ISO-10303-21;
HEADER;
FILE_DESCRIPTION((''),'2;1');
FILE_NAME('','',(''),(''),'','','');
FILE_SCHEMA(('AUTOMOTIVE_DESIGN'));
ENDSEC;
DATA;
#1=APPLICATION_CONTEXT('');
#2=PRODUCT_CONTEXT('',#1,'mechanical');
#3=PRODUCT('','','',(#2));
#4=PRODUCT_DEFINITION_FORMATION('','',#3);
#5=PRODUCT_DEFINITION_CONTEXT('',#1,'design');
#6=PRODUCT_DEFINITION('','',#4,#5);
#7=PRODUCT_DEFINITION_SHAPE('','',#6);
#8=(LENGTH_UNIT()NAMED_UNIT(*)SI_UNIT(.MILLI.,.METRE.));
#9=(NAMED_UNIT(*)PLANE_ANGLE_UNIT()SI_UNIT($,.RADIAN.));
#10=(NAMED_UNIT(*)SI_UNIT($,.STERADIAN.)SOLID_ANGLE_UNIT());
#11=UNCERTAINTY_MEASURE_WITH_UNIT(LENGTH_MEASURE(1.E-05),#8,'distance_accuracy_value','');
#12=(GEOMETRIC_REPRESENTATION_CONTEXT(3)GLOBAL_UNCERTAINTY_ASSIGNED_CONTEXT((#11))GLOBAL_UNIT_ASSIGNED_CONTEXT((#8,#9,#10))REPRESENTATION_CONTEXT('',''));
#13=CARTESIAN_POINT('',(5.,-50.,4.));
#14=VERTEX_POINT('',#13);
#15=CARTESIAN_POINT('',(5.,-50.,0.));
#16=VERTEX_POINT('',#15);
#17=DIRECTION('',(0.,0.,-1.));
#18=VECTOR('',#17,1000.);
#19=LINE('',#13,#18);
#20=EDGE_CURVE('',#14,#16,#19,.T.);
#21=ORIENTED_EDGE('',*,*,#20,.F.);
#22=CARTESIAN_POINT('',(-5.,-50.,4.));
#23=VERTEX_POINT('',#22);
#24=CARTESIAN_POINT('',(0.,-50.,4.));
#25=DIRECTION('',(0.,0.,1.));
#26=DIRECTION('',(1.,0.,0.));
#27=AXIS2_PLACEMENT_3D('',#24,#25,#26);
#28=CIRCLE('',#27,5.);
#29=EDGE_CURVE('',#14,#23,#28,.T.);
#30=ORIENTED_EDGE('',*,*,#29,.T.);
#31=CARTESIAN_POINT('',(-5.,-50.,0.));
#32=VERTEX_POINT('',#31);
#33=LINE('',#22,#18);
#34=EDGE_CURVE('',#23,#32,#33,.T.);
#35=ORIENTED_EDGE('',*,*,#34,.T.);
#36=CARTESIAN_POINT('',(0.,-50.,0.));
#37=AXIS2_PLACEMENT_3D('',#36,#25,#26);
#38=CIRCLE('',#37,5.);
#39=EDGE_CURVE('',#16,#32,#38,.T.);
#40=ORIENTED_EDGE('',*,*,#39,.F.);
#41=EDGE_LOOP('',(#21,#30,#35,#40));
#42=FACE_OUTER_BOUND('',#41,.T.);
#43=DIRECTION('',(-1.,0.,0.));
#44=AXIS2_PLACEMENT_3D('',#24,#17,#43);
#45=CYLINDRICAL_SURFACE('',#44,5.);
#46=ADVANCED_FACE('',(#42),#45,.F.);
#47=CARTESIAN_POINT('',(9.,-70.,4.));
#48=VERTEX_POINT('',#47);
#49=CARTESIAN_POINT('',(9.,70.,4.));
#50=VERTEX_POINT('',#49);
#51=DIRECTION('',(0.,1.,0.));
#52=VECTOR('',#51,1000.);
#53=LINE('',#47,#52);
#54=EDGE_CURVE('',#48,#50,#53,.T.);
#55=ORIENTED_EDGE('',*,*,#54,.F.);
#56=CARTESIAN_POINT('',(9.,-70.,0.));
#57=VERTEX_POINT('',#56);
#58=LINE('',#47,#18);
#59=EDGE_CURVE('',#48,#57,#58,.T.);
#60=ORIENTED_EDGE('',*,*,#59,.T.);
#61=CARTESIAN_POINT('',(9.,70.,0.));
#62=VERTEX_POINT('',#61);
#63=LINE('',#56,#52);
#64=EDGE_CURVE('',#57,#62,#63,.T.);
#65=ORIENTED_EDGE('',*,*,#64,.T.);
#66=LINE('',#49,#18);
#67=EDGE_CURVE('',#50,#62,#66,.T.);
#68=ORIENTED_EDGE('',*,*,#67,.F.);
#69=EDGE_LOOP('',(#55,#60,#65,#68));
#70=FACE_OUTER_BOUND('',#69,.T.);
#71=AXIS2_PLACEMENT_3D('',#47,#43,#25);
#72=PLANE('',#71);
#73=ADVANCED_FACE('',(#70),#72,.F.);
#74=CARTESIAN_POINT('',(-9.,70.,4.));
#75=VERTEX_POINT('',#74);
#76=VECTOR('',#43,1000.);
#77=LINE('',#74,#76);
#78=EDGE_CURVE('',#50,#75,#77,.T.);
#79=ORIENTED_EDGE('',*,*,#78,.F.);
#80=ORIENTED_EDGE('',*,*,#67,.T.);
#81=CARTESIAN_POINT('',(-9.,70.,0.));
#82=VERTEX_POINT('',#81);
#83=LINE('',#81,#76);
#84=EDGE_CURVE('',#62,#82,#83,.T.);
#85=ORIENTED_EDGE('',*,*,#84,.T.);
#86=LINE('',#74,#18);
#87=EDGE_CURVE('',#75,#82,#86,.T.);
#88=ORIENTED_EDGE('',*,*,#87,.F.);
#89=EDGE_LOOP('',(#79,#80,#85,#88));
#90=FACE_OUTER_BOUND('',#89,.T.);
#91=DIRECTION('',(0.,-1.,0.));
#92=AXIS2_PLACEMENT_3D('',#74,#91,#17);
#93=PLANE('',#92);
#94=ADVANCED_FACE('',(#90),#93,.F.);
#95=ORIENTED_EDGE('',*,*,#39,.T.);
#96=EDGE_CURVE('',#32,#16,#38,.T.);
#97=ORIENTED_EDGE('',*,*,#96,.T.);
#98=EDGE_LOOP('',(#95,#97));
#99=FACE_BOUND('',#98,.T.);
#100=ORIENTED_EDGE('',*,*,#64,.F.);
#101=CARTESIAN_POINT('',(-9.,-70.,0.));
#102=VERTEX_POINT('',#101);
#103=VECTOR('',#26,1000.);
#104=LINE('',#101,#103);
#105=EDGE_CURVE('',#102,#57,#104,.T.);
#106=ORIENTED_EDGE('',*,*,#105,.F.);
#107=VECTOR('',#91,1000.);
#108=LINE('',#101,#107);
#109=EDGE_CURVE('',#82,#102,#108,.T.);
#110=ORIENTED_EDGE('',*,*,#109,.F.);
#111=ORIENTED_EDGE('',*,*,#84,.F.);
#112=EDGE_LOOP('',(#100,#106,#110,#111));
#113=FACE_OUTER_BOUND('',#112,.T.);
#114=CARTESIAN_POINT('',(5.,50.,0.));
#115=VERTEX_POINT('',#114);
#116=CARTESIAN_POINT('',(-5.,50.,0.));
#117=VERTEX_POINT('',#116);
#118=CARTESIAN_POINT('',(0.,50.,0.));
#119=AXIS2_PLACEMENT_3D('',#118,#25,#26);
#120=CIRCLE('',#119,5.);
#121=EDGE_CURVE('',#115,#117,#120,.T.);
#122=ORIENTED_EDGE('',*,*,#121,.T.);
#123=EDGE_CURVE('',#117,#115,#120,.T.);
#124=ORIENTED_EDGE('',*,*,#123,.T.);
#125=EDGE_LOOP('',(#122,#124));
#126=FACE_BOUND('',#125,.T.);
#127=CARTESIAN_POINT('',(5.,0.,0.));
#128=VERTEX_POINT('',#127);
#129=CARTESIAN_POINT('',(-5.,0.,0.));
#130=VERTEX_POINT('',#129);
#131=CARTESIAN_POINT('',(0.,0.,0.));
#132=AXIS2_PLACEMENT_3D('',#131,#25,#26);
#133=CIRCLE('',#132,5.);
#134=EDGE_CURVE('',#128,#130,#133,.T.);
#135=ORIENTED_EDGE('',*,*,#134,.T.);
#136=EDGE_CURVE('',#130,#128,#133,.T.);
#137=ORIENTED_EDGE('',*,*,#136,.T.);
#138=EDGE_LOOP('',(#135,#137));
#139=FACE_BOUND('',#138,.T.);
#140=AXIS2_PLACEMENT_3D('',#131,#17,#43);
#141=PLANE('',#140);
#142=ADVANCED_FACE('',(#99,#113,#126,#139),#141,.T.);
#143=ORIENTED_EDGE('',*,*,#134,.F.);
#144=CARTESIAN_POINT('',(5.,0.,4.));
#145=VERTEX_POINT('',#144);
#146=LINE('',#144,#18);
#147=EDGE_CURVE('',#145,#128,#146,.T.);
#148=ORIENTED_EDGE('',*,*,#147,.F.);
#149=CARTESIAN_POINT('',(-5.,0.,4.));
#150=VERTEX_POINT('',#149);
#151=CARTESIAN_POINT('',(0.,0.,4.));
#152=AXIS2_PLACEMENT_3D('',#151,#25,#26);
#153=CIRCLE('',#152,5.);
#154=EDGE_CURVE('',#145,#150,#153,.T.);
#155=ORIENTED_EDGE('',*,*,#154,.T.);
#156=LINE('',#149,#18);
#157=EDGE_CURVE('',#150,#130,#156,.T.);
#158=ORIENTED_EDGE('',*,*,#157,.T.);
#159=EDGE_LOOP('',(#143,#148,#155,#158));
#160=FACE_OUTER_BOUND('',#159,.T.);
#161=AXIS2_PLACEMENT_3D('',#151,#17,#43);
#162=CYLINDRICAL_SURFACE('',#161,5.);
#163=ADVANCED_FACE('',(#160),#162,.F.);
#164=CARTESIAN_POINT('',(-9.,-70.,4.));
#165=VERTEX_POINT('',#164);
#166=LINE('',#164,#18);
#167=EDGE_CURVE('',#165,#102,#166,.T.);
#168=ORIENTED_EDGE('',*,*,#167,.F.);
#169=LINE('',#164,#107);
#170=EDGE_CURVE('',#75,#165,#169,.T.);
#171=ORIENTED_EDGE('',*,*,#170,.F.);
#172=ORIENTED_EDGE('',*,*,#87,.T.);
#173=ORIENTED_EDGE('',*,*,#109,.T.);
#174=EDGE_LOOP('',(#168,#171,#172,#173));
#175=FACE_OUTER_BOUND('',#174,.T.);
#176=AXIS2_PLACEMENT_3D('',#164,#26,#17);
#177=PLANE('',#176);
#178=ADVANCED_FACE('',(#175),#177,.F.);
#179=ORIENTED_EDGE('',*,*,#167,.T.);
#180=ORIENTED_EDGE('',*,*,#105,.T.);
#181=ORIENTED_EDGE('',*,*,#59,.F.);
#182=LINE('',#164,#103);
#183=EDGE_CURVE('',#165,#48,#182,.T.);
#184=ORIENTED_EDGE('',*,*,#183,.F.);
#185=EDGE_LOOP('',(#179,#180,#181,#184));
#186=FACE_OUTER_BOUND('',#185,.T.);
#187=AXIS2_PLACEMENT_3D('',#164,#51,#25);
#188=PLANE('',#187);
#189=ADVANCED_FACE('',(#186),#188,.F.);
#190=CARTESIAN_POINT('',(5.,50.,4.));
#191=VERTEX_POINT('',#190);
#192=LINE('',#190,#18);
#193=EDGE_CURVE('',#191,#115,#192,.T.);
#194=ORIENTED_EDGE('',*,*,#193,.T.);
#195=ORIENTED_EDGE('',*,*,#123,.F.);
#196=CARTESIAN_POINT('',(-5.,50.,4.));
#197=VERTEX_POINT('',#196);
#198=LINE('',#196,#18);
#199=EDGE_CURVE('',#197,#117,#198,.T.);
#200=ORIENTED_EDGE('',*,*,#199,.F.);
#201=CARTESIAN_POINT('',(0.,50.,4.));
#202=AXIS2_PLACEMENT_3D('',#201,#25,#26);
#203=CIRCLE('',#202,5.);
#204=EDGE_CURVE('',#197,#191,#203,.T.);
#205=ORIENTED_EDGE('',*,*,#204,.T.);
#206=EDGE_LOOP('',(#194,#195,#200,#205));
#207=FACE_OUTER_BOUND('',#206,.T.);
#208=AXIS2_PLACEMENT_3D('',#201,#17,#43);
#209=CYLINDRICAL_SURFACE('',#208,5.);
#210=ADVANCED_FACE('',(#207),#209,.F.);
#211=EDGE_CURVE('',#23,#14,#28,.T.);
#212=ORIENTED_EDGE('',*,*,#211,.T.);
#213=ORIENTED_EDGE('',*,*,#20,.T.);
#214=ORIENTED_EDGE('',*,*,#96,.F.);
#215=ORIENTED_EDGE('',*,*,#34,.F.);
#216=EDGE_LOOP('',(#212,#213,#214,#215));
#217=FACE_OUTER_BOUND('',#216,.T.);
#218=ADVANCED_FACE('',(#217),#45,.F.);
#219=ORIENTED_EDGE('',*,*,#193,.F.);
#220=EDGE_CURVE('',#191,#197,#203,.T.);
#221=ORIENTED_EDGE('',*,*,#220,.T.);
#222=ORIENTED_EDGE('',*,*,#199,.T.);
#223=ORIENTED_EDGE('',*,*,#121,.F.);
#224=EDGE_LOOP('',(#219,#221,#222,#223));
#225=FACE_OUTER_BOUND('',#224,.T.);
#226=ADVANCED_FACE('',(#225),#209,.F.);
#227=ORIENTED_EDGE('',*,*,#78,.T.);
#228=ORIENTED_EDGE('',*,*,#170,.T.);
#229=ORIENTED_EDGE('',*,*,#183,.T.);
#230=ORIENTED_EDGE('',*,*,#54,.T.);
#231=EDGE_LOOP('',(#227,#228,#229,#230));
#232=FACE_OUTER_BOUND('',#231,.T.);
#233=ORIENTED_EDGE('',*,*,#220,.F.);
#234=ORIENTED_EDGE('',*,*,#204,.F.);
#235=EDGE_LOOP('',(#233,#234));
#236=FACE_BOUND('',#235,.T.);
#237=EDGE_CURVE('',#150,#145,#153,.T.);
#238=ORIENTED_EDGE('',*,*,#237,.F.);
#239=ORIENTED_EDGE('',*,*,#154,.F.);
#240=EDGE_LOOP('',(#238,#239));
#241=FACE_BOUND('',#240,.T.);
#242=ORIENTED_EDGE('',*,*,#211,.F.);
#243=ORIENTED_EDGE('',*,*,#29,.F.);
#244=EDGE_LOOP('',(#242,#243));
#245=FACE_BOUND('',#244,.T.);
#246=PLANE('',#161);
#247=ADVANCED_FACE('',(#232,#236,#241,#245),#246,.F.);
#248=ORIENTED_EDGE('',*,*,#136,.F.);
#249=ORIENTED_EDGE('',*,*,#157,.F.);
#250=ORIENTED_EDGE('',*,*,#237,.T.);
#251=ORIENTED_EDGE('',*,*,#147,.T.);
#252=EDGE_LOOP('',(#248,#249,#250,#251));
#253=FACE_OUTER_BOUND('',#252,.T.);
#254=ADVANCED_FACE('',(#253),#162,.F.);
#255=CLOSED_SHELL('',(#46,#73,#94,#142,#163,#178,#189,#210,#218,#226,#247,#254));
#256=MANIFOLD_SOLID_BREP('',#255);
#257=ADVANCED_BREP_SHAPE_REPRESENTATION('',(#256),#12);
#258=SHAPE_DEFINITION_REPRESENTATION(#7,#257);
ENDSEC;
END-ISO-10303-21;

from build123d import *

# Parameters (mm, degrees)
SKETCH_1_W          = 18
SKETCH_1_H          = 140
SKETCH_1_R          = 5
BOSS_EXTRUDE1_DEPTH = 4


with BuildPart() as part:
    # Sketch 1 → Boss-Extrude1 (new body)
    with BuildSketch(Plane.XY):
        Rectangle(SKETCH_1_W, SKETCH_1_H)
        with Locations((0, 50)):
            Circle(SKETCH_1_R, mode=Mode.SUBTRACT)
        Circle(SKETCH_1_R, mode=Mode.SUBTRACT)
        with Locations((0, -50)):
            Circle(SKETCH_1_R, mode=Mode.SUBTRACT)
    extrude(amount=BOSS_EXTRUDE1_DEPTH)


solid = part.part
